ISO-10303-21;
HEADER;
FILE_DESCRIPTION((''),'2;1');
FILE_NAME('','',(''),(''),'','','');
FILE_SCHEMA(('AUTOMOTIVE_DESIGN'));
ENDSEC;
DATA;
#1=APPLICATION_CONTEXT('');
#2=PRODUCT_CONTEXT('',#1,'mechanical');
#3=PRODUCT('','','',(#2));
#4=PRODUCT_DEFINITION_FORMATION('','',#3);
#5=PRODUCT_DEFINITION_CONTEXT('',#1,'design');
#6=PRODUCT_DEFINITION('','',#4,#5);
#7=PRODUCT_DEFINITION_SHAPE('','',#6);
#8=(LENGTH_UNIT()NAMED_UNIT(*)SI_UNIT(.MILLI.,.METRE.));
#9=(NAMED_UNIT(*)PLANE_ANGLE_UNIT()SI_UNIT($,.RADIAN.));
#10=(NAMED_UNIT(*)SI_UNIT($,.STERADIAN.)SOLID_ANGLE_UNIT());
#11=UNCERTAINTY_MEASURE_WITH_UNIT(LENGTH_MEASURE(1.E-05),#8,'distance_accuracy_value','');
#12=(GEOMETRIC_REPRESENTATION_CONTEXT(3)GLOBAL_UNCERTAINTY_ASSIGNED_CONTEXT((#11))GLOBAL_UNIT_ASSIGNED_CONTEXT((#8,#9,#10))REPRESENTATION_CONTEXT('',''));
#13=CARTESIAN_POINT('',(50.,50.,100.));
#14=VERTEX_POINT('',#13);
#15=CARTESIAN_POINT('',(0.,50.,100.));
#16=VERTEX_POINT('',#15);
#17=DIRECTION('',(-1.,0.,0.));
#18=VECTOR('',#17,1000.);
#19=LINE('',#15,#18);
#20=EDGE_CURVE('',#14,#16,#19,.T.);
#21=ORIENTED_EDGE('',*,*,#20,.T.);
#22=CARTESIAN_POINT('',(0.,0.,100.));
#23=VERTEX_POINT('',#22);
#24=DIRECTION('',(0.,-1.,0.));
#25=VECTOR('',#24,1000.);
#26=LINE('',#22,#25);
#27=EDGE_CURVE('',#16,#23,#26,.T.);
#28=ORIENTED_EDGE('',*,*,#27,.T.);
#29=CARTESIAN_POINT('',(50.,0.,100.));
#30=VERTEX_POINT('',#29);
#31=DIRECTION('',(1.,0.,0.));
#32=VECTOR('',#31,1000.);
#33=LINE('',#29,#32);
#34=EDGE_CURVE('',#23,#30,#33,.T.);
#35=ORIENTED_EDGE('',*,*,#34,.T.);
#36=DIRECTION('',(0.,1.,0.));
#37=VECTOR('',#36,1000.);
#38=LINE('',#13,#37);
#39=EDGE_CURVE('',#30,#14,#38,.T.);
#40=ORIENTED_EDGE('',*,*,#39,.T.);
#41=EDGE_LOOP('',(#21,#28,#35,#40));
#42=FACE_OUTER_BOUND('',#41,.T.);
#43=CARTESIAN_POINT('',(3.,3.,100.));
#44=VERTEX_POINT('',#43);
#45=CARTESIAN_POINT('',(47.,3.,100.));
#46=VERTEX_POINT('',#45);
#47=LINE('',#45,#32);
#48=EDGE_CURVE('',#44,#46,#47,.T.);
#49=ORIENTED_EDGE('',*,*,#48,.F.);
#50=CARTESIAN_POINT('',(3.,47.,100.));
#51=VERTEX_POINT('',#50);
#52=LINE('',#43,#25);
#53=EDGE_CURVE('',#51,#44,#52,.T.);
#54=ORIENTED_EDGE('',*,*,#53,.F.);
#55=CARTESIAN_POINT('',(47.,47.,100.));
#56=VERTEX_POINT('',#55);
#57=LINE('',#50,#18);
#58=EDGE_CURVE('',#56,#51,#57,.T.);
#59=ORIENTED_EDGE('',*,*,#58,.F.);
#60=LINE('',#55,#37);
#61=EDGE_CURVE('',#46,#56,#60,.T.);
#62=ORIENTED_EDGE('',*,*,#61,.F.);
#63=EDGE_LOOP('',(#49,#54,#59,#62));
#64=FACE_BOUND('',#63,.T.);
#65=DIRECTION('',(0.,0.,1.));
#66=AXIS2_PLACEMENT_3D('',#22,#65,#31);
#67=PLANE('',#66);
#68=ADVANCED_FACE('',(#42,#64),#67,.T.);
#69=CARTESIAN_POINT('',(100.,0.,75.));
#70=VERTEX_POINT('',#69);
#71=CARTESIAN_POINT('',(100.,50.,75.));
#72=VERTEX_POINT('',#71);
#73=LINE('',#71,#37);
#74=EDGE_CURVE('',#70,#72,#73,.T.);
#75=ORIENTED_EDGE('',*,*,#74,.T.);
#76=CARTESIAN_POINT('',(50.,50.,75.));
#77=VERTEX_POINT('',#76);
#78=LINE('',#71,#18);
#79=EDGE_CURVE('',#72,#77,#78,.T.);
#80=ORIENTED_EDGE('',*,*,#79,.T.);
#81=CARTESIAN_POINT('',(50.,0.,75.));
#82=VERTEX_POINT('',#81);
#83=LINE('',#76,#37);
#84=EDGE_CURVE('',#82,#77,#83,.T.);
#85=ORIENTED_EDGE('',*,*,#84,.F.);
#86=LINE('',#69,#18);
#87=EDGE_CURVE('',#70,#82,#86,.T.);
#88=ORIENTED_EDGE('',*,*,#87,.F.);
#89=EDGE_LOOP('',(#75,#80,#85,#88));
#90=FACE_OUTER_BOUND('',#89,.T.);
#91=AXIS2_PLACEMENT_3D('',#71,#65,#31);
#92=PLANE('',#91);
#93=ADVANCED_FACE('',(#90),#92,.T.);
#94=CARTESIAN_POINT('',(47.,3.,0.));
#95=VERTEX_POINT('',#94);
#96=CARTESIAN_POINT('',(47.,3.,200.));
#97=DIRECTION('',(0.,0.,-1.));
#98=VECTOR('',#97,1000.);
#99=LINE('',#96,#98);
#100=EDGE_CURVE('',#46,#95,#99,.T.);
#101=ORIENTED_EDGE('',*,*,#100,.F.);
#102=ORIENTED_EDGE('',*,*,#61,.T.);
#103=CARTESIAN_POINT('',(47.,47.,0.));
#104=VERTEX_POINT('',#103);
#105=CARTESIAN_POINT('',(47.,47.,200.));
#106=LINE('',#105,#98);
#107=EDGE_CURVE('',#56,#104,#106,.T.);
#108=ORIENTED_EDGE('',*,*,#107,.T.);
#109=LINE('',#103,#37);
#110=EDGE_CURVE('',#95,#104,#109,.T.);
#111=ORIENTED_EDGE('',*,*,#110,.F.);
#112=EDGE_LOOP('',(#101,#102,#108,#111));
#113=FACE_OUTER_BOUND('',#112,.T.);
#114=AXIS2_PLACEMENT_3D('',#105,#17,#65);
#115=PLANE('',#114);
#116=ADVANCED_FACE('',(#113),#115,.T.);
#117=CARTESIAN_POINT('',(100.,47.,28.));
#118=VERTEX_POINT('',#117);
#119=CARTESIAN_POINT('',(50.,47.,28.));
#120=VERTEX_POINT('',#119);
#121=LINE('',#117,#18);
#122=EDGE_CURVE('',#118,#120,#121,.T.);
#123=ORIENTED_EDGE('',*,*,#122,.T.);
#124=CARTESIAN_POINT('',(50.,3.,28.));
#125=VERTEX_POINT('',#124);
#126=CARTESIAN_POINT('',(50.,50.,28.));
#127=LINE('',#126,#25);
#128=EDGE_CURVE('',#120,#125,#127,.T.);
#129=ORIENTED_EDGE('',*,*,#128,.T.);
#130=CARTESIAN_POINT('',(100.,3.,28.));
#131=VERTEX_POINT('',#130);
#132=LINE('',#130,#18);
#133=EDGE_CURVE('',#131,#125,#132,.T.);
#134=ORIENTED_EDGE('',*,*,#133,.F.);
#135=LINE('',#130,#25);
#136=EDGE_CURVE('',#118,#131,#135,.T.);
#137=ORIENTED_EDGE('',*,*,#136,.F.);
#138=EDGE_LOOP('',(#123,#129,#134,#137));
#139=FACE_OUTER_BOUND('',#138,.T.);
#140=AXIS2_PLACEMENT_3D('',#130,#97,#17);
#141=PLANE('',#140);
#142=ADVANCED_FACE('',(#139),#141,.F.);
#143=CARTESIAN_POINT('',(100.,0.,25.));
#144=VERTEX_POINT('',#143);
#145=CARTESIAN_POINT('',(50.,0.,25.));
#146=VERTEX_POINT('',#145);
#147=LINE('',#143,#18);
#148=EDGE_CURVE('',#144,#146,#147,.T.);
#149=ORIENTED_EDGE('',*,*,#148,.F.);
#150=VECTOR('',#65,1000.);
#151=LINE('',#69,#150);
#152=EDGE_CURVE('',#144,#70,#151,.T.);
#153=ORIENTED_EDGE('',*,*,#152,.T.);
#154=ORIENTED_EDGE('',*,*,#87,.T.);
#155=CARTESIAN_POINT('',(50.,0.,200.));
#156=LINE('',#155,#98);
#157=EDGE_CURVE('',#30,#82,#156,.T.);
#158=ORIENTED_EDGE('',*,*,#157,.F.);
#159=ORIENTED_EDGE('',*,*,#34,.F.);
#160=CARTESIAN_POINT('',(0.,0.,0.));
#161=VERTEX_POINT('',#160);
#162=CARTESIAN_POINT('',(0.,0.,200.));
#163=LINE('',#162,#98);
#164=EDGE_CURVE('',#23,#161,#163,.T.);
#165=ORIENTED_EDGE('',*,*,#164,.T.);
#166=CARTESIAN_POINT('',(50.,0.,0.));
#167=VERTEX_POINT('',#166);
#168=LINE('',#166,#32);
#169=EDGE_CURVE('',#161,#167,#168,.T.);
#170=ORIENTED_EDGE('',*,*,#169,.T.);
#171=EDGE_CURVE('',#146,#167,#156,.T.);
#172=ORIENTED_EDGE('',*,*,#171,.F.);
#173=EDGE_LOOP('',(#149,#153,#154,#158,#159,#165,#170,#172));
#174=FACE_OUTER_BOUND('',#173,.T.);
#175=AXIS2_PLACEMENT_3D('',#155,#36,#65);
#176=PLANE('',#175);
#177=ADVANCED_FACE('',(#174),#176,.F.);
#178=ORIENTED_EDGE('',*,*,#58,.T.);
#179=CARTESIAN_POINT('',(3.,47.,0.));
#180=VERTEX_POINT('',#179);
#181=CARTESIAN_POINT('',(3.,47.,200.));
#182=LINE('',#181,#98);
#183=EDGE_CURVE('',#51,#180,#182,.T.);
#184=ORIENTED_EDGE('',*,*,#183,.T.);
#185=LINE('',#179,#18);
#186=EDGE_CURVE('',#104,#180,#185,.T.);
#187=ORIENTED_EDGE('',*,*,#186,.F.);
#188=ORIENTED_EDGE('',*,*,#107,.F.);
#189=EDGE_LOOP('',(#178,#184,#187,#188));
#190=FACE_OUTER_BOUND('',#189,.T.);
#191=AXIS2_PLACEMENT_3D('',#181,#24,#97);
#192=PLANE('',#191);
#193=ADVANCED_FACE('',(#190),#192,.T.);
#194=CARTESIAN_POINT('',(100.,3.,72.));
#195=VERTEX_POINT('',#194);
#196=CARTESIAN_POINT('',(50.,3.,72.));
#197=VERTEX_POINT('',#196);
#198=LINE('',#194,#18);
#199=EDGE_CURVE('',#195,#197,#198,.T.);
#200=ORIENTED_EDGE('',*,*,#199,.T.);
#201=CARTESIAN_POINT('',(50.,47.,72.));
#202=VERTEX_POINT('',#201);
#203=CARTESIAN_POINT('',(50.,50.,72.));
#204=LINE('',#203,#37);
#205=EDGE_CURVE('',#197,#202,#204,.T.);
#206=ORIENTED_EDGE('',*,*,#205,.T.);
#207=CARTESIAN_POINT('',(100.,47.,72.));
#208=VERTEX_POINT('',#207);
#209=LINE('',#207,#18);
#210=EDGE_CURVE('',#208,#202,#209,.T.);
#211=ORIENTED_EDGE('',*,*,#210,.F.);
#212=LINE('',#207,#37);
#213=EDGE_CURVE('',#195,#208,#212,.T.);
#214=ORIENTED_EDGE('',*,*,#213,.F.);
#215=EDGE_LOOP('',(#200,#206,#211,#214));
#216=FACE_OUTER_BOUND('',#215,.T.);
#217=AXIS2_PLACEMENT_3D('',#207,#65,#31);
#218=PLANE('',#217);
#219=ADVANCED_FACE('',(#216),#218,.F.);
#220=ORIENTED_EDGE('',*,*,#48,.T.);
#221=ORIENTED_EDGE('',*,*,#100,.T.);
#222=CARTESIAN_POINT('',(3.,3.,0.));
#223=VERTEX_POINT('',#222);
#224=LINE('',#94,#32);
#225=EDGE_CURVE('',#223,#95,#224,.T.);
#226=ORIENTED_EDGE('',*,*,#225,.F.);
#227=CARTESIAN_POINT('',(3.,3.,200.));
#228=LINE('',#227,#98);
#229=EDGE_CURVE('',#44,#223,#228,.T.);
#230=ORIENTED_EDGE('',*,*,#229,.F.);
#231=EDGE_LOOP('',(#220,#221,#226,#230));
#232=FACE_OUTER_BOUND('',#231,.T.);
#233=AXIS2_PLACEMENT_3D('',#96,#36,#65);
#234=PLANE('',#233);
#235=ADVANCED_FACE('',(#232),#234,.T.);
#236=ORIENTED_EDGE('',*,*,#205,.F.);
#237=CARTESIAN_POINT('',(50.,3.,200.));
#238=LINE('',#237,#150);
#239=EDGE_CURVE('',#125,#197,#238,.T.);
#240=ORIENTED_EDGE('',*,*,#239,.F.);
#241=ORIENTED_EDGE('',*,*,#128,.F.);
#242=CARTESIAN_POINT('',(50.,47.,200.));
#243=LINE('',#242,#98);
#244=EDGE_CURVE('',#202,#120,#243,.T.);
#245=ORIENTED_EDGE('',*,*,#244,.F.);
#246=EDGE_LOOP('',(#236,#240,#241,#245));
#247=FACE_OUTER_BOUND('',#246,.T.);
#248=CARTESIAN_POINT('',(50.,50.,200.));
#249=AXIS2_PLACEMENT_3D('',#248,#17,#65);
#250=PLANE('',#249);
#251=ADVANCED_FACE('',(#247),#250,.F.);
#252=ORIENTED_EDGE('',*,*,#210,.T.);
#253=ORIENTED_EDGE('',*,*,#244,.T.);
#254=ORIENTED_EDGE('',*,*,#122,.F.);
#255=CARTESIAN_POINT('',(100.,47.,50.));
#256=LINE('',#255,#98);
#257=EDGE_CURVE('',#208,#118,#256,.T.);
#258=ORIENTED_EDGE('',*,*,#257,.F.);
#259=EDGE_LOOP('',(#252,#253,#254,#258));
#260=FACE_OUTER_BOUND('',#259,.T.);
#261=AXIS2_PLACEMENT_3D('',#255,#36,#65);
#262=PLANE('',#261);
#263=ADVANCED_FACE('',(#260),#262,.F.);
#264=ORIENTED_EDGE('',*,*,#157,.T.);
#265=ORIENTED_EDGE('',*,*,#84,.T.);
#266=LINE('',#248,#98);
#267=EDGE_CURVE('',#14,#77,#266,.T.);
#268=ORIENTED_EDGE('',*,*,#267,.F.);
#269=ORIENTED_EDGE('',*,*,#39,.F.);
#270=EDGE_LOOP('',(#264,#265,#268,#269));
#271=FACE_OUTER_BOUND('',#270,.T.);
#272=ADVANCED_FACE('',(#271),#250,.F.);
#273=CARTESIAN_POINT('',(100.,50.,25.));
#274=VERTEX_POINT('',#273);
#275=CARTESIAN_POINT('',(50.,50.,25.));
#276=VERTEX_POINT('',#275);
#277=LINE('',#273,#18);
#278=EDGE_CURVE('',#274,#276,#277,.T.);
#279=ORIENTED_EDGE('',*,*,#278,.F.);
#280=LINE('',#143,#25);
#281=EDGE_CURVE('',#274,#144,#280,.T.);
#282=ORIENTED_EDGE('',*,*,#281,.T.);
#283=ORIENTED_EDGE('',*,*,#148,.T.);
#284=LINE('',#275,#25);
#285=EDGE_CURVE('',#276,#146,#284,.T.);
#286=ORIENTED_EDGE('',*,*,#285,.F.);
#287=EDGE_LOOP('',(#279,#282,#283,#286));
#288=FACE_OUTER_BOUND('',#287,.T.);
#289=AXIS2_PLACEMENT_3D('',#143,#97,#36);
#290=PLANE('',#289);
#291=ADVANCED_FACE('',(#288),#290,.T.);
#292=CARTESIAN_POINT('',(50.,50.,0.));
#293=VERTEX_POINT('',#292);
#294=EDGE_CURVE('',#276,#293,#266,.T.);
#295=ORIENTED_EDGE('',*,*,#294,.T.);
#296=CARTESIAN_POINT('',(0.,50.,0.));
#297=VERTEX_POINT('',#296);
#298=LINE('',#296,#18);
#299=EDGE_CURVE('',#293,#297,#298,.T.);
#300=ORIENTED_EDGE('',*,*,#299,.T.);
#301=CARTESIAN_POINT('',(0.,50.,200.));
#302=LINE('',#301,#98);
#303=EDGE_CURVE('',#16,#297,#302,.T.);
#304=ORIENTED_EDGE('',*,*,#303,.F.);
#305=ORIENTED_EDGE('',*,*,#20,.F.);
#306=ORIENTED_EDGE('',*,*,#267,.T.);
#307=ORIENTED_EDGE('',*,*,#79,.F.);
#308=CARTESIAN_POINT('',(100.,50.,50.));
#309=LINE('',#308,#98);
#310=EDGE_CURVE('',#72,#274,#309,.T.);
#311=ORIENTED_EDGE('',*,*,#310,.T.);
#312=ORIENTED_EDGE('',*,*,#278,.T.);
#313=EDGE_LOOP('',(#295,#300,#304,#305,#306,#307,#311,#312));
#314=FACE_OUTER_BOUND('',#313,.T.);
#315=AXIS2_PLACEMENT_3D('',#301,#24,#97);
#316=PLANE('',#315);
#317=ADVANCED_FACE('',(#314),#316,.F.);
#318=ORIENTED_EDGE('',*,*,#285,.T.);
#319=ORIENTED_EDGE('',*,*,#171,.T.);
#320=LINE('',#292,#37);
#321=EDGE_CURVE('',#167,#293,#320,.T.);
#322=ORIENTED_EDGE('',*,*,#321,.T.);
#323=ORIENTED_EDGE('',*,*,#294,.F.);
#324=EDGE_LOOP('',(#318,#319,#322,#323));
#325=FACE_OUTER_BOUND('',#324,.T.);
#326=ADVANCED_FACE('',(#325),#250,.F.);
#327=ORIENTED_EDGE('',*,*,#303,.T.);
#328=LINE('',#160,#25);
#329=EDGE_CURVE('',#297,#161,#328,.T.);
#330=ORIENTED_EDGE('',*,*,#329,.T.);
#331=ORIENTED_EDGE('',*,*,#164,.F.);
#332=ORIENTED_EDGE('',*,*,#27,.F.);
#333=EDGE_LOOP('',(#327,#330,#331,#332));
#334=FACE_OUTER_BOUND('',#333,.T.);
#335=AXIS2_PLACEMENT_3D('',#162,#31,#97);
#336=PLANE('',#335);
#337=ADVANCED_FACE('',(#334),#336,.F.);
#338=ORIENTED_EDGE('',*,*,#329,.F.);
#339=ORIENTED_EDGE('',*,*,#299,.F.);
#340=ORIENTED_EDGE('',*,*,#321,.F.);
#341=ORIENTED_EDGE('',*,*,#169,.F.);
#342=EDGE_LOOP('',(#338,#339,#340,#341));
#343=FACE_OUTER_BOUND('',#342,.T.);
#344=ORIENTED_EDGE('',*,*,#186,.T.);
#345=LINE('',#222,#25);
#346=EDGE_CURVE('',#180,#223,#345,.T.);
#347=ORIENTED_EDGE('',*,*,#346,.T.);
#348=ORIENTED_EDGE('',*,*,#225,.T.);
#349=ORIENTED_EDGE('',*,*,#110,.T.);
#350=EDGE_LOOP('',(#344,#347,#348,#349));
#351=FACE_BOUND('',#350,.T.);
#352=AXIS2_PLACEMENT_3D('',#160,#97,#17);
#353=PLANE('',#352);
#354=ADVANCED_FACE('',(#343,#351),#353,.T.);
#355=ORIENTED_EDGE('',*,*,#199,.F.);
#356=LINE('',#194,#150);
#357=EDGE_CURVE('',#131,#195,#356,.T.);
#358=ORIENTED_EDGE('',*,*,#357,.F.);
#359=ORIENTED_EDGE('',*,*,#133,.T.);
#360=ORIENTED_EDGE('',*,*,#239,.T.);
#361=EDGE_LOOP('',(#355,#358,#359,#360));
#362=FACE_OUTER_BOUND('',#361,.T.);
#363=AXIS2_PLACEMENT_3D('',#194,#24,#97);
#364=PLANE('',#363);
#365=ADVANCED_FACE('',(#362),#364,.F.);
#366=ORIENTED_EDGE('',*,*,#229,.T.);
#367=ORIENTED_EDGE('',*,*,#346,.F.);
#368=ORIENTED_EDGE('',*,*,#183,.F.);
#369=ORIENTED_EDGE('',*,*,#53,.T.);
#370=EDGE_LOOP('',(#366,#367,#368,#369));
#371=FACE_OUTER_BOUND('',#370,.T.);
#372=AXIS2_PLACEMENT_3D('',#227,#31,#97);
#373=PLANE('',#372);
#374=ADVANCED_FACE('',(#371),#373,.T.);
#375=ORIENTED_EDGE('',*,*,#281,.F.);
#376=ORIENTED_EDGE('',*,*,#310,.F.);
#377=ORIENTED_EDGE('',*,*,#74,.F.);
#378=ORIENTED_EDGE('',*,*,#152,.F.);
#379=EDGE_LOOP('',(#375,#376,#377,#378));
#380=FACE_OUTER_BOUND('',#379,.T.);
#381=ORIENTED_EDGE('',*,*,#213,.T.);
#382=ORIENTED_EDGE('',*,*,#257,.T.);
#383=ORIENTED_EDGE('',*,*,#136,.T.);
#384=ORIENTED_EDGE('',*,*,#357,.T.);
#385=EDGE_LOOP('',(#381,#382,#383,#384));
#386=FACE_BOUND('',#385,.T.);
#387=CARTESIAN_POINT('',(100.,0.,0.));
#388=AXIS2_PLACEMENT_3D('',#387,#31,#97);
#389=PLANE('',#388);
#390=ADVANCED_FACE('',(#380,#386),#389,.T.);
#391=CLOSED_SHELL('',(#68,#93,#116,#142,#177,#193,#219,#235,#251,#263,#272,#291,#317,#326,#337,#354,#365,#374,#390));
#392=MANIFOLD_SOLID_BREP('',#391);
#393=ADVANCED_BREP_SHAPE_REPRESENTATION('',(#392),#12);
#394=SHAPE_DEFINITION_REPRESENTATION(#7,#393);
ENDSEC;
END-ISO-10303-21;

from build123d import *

# Parameters (mm, degrees)
SKETCH_1_W          = 50
SKETCH_1_H          = 50
SKETCH_1_W_2        = 44
SKETCH_1_H_2        = 44
EXTRUDE_1_DEPTH     = 200
SKETCH_2_W          = 56
SKETCH_2_H          = 56
CUT_EXTRUDE_1_DEPTH = 100
EXTRUDE_3_DEPTH     = 100
SKETCH_4_W          = 44
SKETCH_4_H          = 44
CUT_EXTRUDE_2_DEPTH = 100


with BuildPart() as part:
    # 草图1 → 凸台-拉伸1 (new body)
    with BuildSketch(Plane.XY):
        with Locations((25, 25)):
            Rectangle(SKETCH_1_W, SKETCH_1_H)
        with Locations((25, 25)):
            Rectangle(SKETCH_1_W_2, SKETCH_1_H_2, mode=Mode.SUBTRACT)
    extrude(amount=EXTRUDE_1_DEPTH)

    # 草图2 → 切除-拉伸1 (cut)
    with BuildSketch(Plane.XY.offset(200)):
        with Locations((25, 25)):
            Rectangle(SKETCH_2_W, SKETCH_2_H)
    extrude(amount=-CUT_EXTRUDE_1_DEPTH, mode=Mode.SUBTRACT)

    # 草图3 → 凸台-拉伸3 (add)
    with BuildSketch(Plane.ZY):
        Polygon((50, 50), (25, 50), (25, 0), (75, 0), (75, 50), align=None)
        Polygon((50, 47), (28, 47), (28, 3), (72, 3), (72, 47), align=None, mode=Mode.SUBTRACT)
    extrude(amount=-EXTRUDE_3_DEPTH)

    # 草图4 → 切除-拉伸2 (cut)
    with BuildSketch(Plane(origin=(0, 0, 0), x_dir=(-1, 0, 0), z_dir=(0, 0, -1))):
        with Locations((-25, 25)):
            Rectangle(SKETCH_4_W, SKETCH_4_H)
    extrude(amount=-CUT_EXTRUDE_2_DEPTH, mode=Mode.SUBTRACT)


solid = part.part
